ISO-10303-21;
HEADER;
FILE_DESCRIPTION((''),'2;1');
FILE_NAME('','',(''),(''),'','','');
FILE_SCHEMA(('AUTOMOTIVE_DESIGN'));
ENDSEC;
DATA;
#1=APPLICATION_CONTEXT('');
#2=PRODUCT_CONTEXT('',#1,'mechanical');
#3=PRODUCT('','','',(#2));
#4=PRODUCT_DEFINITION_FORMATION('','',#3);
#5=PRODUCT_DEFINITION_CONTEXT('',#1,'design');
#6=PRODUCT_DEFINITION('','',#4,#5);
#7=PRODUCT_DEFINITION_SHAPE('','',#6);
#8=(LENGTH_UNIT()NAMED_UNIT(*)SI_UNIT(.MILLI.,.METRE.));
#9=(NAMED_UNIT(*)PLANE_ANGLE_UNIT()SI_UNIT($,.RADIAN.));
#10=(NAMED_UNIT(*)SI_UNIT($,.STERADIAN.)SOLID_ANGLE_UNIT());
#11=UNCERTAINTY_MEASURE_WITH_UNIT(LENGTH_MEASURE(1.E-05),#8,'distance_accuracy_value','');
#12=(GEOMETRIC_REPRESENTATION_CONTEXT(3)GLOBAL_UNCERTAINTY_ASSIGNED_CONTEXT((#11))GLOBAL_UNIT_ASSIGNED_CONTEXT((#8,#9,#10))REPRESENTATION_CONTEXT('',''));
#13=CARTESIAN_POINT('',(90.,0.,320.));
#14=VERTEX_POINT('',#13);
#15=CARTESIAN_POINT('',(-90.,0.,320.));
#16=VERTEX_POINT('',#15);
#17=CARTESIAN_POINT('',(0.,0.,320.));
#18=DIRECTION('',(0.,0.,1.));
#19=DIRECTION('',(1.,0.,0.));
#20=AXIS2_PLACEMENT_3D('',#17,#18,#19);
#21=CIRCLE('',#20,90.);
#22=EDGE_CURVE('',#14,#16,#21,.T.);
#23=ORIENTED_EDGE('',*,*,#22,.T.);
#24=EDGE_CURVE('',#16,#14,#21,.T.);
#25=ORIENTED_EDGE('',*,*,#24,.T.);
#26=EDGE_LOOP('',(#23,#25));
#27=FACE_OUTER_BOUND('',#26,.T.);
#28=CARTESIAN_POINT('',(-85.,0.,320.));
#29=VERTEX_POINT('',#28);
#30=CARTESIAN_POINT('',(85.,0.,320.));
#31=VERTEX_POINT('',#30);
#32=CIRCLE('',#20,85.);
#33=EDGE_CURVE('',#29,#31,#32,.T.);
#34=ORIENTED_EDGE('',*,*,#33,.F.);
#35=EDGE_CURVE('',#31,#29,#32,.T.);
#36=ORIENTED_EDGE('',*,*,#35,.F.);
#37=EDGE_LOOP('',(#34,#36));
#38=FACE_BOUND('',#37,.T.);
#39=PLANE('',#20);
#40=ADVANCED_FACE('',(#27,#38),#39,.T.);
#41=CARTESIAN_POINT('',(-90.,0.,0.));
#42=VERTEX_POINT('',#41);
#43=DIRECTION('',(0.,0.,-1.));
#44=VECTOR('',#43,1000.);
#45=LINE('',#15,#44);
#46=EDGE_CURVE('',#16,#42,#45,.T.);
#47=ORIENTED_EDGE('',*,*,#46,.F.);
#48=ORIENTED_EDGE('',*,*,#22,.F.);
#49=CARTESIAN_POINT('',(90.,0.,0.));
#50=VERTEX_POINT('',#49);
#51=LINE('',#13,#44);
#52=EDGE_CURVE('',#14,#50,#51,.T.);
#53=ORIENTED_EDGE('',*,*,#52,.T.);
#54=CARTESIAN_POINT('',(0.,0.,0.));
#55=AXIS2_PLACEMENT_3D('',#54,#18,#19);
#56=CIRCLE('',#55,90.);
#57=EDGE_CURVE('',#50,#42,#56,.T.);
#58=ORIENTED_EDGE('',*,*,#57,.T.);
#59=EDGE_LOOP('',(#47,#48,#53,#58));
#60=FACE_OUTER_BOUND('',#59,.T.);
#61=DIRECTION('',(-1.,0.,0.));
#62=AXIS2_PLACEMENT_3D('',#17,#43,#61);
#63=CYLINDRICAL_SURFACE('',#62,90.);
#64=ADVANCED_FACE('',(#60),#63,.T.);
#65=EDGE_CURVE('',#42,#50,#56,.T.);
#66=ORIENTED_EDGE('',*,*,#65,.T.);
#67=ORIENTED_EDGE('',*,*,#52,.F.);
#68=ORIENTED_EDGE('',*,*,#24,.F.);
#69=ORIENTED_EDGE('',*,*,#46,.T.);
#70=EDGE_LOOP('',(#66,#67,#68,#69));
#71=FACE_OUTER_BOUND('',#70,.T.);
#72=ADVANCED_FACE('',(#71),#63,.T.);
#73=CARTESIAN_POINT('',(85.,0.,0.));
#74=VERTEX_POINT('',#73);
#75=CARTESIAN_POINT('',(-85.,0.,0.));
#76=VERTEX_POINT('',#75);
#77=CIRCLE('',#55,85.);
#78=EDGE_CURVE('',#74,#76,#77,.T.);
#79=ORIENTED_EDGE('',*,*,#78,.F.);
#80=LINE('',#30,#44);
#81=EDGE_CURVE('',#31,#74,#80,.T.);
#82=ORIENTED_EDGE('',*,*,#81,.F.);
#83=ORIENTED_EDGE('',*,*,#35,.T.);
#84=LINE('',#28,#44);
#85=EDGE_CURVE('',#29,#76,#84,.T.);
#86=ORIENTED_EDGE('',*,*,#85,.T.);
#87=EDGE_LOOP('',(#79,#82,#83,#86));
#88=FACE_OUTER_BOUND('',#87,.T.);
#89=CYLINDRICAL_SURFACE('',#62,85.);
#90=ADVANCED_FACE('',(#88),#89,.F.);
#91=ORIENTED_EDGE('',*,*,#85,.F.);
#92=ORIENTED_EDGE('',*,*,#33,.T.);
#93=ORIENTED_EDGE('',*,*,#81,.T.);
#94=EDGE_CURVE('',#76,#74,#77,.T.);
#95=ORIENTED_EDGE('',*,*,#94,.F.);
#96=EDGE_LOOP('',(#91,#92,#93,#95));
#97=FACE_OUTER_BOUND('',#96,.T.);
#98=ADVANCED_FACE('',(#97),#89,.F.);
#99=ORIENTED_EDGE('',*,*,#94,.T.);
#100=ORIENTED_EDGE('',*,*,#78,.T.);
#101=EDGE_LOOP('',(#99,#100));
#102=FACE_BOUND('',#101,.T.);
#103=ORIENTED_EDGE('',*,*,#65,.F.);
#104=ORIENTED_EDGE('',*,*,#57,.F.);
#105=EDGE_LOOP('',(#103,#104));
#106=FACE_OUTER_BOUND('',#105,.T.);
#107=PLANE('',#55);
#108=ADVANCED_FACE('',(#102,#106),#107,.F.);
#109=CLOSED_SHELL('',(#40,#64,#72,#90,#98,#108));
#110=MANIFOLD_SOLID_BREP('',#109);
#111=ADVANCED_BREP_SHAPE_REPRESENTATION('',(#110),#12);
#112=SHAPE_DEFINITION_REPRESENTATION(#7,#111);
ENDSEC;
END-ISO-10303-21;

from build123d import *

# Parameters (mm, degrees)
SKETCH_1_R      = 90
SKETCH_1_R_2    = 85
EXTRUDE_2_DEPTH = 320


with BuildPart() as part:
    # 草图1 → 凸台-拉伸2 (new body)
    with BuildSketch(Plane.XY):
        Circle(SKETCH_1_R)
        Circle(SKETCH_1_R_2, mode=Mode.SUBTRACT)
    extrude(amount=EXTRUDE_2_DEPTH)


solid = part.part
